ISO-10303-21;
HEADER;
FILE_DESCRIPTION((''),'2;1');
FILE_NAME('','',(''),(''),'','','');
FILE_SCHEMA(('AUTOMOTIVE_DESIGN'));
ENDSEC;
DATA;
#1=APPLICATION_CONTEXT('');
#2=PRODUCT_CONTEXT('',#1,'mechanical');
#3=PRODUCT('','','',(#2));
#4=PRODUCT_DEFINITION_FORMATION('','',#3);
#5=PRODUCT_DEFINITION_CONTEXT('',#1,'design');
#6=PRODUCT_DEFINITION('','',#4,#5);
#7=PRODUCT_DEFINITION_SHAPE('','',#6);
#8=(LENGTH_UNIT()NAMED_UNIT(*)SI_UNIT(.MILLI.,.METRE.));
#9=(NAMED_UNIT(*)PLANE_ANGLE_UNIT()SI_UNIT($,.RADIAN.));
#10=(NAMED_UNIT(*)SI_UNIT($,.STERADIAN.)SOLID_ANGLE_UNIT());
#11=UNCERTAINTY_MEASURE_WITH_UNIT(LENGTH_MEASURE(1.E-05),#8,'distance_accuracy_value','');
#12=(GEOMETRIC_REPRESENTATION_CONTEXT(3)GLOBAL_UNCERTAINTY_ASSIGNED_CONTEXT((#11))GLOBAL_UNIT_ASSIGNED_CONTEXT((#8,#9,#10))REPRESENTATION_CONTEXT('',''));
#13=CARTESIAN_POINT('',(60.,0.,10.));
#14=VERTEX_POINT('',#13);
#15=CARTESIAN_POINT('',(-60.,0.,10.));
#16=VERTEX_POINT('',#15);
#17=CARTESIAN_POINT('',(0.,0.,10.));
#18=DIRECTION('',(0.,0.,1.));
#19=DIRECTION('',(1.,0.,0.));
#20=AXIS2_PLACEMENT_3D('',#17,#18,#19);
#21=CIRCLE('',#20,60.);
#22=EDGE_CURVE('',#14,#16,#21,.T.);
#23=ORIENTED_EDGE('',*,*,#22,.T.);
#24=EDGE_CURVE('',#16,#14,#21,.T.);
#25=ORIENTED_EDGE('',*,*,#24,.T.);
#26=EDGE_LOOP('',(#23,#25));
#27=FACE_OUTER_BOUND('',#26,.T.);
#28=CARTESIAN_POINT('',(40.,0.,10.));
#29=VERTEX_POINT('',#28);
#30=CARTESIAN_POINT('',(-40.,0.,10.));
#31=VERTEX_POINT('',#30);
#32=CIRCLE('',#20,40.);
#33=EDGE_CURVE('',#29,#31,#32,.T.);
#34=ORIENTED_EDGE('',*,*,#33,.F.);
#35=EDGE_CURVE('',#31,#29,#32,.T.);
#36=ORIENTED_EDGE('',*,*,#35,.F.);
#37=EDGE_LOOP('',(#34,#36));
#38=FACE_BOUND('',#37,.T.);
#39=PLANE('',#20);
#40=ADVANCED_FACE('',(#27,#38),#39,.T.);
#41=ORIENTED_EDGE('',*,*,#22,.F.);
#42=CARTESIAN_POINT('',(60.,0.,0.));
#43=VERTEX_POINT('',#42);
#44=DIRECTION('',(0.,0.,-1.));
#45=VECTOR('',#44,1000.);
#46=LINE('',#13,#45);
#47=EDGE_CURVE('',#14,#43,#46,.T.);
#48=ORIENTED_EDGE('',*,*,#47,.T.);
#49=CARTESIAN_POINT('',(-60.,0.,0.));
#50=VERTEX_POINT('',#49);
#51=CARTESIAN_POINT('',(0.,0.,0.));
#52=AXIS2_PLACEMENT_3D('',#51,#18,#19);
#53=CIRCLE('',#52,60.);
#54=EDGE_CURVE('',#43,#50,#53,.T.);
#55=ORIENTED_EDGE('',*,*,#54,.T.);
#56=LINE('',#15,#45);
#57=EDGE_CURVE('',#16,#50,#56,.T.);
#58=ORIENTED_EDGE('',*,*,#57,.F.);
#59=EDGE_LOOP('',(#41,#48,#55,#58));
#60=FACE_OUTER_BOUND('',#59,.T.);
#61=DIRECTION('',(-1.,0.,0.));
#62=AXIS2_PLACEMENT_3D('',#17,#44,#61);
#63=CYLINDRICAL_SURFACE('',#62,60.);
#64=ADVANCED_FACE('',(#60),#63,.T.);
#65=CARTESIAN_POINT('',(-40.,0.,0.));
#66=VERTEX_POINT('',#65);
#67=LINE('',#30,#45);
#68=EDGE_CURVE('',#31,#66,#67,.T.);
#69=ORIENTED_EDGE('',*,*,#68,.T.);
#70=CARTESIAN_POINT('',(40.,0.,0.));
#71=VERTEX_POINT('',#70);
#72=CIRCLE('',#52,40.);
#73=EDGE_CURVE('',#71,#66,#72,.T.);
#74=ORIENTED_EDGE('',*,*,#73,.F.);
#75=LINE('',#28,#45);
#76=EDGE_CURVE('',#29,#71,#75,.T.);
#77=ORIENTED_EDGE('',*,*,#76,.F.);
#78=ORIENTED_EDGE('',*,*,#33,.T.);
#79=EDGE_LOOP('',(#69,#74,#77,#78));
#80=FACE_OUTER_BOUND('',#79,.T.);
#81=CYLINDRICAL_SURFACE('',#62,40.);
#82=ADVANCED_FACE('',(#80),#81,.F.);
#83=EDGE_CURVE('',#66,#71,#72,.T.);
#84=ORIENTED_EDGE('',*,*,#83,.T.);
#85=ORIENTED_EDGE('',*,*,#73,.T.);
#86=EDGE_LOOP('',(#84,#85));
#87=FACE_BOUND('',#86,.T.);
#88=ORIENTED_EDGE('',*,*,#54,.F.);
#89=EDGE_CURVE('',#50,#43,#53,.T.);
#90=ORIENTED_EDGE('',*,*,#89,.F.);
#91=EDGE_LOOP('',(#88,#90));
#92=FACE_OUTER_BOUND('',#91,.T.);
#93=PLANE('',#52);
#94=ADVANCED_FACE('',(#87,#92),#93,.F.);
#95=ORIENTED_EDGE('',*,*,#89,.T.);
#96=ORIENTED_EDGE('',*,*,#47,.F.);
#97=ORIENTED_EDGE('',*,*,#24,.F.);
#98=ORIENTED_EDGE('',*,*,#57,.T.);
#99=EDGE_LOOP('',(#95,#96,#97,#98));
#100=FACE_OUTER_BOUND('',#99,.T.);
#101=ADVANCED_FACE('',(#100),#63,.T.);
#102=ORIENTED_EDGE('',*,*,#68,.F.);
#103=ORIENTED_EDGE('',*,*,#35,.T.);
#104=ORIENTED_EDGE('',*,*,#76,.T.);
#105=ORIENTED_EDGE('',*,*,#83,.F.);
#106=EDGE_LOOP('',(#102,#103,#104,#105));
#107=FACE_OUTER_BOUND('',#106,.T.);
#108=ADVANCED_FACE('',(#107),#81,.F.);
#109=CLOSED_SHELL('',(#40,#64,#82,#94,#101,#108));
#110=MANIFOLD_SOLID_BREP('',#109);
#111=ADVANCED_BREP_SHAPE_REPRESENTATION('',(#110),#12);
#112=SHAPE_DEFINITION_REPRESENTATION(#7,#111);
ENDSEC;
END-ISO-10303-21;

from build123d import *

# Parameters (mm, degrees)
SKETCH1_R           = 60
SKETCH1_R_2         = 40
BOSS_EXTRUDE1_DEPTH = 10


with BuildPart() as part:
    # Sketch1 → Boss-Extrude1 (new body)
    with BuildSketch(Plane.XY):
        Circle(SKETCH1_R)
        Circle(SKETCH1_R_2, mode=Mode.SUBTRACT)
    extrude(amount=BOSS_EXTRUDE1_DEPTH)


solid = part.part
